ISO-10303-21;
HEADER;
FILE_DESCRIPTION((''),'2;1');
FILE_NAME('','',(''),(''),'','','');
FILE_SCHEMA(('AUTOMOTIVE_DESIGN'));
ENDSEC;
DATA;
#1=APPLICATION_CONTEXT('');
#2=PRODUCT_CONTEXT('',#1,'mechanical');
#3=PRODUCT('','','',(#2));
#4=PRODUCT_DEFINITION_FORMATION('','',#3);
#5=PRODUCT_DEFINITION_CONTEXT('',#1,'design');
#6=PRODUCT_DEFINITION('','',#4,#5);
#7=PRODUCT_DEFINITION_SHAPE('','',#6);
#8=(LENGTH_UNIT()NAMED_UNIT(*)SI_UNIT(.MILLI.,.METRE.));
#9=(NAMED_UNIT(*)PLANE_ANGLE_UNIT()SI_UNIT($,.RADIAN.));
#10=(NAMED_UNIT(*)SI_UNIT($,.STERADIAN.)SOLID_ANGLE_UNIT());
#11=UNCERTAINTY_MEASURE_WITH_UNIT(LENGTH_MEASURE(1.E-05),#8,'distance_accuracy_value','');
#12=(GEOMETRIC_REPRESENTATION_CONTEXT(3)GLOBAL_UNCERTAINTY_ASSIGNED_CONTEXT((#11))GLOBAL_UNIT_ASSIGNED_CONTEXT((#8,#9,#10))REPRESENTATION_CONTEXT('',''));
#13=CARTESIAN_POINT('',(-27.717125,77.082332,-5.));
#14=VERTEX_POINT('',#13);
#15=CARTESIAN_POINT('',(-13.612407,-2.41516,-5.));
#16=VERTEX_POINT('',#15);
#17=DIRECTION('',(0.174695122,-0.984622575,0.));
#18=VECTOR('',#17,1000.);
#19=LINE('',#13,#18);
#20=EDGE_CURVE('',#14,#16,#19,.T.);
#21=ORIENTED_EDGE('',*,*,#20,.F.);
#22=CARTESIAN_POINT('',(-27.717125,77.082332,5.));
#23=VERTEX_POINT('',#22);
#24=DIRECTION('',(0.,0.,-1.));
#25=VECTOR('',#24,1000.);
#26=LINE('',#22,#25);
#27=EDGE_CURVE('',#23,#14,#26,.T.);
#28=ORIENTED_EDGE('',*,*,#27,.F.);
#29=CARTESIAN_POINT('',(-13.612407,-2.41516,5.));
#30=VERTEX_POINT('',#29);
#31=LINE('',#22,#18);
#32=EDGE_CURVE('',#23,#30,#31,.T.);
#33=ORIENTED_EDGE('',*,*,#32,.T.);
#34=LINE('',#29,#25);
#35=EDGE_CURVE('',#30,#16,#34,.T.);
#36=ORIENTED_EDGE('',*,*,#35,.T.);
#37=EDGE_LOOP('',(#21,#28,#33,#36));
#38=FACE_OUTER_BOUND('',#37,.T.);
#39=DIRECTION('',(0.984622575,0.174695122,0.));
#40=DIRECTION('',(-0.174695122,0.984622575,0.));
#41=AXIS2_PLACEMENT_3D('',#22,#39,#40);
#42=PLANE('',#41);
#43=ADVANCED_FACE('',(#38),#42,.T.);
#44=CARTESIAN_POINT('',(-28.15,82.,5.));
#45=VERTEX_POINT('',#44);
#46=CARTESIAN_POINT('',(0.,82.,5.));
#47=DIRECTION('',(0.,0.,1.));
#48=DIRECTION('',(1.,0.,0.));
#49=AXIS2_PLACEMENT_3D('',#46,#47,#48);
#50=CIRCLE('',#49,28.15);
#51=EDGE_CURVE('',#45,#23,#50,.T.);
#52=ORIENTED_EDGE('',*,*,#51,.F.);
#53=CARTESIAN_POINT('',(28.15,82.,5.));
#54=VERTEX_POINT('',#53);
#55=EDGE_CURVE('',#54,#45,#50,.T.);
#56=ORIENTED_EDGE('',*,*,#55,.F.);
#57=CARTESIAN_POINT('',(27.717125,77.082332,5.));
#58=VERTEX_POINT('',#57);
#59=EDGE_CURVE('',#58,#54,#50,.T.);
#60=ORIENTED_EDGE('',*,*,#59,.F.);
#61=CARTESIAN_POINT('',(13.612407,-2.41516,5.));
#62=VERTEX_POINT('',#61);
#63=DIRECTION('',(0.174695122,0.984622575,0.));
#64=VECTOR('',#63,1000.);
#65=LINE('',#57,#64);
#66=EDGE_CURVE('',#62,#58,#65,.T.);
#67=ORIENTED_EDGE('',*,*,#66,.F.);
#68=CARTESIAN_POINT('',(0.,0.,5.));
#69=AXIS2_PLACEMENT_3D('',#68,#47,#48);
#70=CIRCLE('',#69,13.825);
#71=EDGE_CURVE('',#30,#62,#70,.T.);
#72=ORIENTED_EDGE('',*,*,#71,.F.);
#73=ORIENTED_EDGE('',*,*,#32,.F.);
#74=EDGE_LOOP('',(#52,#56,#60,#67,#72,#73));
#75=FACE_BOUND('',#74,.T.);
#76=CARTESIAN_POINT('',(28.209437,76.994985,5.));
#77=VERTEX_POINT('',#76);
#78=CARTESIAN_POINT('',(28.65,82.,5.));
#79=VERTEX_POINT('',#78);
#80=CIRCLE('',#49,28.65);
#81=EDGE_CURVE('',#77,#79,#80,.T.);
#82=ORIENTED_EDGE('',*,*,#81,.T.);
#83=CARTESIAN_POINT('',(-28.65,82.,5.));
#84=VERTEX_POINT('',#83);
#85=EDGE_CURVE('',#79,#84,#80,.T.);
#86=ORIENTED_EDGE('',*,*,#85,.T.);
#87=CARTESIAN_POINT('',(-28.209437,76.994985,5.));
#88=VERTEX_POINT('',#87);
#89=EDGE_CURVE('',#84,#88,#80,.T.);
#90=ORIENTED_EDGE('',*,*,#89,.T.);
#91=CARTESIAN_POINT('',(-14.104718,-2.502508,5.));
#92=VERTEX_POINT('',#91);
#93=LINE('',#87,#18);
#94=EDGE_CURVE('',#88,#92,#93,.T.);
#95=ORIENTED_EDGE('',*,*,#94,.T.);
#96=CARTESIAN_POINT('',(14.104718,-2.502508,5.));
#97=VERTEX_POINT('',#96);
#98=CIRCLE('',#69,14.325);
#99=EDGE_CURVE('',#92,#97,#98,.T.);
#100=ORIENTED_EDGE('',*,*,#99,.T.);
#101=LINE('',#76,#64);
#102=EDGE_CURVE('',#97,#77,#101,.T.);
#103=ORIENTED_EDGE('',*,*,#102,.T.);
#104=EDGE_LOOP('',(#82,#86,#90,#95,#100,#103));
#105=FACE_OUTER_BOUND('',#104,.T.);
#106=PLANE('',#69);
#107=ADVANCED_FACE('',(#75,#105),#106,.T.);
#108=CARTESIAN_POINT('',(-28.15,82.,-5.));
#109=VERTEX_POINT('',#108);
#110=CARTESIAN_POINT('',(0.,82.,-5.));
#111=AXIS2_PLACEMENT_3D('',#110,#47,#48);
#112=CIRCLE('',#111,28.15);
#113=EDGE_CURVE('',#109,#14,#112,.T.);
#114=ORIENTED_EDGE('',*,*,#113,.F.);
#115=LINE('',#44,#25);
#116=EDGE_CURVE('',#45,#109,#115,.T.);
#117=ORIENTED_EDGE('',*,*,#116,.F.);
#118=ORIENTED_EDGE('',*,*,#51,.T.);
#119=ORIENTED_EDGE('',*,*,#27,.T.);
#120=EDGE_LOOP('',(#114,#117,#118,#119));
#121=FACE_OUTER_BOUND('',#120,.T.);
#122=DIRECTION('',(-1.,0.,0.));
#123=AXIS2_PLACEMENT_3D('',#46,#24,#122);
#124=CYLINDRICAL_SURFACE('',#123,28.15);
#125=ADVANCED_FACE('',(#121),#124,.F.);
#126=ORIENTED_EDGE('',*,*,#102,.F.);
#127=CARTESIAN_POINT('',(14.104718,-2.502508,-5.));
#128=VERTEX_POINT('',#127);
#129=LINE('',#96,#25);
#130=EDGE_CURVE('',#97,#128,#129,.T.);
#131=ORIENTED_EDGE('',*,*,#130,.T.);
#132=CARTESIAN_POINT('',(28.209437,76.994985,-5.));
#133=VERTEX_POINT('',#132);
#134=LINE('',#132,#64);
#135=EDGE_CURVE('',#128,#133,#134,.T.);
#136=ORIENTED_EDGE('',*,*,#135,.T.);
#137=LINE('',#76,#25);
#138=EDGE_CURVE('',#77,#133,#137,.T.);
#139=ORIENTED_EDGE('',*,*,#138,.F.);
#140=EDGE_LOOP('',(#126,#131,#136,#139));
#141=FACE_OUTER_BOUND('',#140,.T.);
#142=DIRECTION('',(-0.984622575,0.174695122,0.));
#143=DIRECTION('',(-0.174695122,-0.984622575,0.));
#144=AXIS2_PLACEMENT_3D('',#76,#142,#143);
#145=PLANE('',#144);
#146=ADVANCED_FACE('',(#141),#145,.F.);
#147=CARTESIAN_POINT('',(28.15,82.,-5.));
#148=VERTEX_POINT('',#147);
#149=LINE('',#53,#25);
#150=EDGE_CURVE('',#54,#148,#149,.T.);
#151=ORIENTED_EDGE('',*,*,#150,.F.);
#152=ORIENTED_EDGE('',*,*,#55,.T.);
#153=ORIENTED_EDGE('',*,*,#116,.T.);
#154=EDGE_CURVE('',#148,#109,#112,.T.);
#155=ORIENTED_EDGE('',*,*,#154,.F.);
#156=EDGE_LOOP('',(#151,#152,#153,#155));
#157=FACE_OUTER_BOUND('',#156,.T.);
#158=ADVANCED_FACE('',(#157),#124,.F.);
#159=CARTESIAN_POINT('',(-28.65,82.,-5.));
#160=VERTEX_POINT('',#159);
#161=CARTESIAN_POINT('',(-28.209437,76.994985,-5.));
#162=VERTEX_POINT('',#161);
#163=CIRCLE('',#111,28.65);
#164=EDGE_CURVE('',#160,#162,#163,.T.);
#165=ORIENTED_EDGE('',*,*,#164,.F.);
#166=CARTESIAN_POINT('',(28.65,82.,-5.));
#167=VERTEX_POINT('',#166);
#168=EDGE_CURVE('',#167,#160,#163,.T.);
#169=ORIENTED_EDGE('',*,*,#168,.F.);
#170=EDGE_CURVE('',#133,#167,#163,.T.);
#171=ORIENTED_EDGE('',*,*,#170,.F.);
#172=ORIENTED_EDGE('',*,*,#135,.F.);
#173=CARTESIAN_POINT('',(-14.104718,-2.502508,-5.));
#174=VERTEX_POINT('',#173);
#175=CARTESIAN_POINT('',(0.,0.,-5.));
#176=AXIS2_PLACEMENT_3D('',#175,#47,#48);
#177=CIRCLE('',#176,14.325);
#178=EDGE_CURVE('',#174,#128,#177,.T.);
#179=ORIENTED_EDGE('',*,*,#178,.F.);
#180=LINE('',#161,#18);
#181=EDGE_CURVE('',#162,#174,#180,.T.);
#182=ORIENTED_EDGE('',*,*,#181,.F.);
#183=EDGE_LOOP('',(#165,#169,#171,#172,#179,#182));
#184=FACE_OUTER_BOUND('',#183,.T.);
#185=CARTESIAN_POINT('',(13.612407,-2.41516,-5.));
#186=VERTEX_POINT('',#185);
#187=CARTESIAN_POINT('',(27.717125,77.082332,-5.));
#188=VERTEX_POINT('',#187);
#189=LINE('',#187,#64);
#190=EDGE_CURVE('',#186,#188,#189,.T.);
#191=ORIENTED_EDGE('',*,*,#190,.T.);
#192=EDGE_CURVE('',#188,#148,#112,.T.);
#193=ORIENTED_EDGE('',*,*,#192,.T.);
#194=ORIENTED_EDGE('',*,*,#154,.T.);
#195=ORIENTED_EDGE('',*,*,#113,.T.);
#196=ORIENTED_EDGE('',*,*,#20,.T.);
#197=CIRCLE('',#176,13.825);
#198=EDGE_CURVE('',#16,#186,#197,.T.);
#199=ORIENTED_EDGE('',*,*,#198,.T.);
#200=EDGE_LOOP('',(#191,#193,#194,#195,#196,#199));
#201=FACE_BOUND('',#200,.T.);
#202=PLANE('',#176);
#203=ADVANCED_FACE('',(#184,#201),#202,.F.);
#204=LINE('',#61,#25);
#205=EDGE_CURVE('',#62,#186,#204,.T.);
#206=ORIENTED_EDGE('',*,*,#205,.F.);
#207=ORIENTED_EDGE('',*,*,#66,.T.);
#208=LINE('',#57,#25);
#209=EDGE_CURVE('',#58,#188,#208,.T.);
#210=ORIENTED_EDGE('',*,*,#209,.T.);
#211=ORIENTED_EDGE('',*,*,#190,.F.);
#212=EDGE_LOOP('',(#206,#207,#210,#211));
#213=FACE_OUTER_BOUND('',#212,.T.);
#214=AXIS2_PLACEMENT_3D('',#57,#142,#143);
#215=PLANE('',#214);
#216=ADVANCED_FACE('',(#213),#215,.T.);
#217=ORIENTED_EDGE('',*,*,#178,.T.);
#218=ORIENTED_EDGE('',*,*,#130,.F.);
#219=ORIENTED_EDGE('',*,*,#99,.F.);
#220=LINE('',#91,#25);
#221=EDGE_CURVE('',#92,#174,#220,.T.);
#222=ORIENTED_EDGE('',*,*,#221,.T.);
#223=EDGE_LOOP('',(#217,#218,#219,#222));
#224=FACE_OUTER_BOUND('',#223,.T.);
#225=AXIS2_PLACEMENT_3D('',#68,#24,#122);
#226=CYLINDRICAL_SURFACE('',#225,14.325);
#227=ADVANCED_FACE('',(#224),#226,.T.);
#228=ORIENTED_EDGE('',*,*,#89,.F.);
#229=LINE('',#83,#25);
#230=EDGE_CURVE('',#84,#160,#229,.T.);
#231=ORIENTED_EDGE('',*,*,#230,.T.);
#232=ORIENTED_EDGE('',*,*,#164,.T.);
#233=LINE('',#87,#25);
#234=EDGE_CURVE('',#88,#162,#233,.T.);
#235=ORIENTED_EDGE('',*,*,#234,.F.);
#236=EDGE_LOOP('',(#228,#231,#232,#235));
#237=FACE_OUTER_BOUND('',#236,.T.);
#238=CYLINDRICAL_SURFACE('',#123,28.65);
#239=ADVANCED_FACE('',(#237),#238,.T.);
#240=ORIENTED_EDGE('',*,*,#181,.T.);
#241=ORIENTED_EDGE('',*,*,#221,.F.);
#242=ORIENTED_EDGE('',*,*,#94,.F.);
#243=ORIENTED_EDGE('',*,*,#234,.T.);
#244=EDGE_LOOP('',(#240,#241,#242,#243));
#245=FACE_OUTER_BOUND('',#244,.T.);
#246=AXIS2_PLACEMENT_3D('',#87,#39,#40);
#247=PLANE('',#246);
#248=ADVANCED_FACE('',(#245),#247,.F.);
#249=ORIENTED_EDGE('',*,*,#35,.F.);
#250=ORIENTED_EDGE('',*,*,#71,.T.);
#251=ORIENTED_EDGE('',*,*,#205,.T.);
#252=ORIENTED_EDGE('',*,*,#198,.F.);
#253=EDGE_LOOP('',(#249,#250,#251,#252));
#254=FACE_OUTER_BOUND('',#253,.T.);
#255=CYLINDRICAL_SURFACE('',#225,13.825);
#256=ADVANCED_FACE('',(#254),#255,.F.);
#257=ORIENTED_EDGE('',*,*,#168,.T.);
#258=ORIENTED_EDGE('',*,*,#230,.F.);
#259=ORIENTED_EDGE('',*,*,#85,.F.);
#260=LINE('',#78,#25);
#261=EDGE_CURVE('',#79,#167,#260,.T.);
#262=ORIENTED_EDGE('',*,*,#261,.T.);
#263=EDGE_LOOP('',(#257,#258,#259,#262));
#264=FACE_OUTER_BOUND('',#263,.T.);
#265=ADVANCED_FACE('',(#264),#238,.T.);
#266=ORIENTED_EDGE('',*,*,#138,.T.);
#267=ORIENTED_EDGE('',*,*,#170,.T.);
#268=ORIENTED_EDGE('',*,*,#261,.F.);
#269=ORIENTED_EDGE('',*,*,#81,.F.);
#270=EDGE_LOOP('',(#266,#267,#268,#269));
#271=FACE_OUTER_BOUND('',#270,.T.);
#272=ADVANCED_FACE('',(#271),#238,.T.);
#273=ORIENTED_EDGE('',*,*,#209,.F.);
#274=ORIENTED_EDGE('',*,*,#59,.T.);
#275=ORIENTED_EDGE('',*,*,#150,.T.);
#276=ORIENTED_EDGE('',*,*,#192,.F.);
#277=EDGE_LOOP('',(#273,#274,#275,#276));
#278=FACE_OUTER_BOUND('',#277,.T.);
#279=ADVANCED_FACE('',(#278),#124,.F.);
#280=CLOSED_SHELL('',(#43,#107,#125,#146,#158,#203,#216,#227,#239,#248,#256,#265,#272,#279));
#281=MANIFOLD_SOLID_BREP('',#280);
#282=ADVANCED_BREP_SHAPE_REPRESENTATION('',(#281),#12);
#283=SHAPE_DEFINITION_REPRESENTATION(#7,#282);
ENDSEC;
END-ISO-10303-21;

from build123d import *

# Parameters (mm, degrees)
BOSS_EXTRUDE1_DEPTH = 5


with BuildPart() as part:
    # Sketch1 → Boss-Extrude1 (new, symmetric)
    with BuildSketch(Plane.XY):
        with BuildLine():
            Line((-28.209436762, 76.994984756), (-14.104718381, -2.502507622))
            ThreePointArc((-14.104718381, -2.502507622), (0, -14.325), (14.104718381, -2.502507622))
            Line((14.104718381, -2.502507622), (28.209436762, 76.994984756))
            ThreePointArc((28.209436762, 76.994984756), (0, 110.65), (-28.209436762, 76.994984756))
        make_face()
        with BuildLine():
            Line((-27.717125474, 77.082332317), (-13.612407094, -2.415160061))
            ThreePointArc((-13.612407094, -2.415160061), (0, -13.825), (13.612407094, -2.415160061))
            Line((13.612407094, -2.415160061), (27.717125474, 77.082332317))
            ThreePointArc((27.717125474, 77.082332317), (0, 110.15), (-27.717125474, 77.082332317))
        make_face(mode=Mode.SUBTRACT)
    extrude(amount=BOSS_EXTRUDE1_DEPTH, both=True)


solid = part.part
